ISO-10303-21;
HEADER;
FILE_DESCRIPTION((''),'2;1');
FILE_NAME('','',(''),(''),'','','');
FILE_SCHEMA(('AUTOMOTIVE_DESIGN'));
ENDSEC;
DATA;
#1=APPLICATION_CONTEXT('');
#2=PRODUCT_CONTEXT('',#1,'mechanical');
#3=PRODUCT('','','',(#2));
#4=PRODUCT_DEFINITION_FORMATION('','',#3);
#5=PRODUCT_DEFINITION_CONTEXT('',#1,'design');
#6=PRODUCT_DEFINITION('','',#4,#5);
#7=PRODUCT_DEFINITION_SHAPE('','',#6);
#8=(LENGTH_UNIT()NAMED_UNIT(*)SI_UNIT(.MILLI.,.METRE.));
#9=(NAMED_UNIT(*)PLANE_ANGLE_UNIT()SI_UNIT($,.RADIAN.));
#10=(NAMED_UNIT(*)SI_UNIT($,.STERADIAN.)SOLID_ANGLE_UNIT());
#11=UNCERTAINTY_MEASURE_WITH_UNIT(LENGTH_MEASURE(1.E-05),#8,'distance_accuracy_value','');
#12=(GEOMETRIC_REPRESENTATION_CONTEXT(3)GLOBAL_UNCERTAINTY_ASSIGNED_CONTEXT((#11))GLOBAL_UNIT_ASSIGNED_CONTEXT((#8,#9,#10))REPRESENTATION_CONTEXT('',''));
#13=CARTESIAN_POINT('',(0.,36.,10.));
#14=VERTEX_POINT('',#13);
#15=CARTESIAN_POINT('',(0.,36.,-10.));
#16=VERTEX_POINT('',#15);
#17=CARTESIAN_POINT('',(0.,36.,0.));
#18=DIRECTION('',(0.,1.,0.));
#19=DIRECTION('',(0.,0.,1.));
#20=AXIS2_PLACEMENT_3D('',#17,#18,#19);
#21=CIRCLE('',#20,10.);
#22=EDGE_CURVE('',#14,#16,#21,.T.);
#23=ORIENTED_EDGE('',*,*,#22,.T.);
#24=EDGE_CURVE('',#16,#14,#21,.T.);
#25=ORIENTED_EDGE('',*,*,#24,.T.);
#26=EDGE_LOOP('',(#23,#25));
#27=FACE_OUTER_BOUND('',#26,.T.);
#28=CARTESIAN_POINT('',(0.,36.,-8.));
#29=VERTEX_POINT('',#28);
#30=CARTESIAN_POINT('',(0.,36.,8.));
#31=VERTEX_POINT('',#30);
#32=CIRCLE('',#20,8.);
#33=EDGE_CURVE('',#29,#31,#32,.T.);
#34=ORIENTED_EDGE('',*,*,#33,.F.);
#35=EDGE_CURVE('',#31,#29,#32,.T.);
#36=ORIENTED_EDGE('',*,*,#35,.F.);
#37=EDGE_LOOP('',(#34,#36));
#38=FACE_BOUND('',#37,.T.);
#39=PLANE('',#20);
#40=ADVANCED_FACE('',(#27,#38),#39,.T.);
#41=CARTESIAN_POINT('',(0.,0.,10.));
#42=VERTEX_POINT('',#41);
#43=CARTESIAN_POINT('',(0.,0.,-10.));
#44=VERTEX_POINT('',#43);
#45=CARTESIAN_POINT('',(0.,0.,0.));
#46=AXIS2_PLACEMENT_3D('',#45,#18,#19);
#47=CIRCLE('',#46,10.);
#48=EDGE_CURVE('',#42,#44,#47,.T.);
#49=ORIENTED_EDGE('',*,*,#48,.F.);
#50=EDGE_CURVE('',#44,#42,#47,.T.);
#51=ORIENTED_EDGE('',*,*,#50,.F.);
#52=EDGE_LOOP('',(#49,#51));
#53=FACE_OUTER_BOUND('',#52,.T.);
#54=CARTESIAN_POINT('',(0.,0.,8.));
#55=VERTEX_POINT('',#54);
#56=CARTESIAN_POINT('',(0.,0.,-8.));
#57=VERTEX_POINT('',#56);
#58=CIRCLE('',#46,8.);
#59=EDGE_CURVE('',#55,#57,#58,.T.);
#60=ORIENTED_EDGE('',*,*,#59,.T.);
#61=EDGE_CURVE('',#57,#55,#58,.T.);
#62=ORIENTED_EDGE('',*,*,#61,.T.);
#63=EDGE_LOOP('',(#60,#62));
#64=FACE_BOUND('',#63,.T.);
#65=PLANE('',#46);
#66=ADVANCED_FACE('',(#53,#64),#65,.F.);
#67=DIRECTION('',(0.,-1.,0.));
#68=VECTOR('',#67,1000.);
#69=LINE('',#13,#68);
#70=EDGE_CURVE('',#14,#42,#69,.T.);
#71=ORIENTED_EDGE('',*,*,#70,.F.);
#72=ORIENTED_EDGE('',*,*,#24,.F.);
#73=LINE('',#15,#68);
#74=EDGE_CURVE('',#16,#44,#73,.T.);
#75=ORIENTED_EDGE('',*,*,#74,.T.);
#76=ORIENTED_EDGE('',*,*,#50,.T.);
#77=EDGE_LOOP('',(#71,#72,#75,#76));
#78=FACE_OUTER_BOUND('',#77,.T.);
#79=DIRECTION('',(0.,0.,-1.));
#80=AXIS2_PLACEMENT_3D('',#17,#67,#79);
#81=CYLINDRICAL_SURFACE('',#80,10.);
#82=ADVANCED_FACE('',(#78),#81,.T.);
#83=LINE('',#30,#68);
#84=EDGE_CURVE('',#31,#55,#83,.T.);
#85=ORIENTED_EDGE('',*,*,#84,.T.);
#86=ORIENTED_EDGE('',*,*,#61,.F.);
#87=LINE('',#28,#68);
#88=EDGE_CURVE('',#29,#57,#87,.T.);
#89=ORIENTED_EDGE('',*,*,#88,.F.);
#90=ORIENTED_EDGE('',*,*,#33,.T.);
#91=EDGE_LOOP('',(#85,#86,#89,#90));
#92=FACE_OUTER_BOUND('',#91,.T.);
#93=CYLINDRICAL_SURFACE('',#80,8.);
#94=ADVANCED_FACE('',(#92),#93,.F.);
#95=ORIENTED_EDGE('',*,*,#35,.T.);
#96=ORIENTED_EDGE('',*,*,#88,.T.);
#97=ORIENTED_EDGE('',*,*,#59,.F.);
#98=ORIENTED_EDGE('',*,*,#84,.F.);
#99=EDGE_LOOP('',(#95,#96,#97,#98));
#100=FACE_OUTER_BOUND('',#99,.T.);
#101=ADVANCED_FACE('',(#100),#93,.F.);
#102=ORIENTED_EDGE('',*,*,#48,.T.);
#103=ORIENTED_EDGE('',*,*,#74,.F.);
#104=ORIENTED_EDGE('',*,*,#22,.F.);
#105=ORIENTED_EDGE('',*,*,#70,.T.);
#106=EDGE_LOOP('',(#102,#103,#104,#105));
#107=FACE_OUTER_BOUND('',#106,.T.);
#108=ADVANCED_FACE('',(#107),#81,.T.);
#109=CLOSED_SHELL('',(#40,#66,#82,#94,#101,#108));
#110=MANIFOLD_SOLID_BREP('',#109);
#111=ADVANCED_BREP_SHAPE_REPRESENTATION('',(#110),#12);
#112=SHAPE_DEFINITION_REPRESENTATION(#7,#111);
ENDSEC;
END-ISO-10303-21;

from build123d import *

# Parameters (mm, degrees)
SKETCH1_R           = 10
SKETCH1_R_2         = 8
BOSS_EXTRUDE1_DEPTH = 36


with BuildPart() as part:
    # Sketch1 → Boss-Extrude1 (new body)
    with BuildSketch(Plane(origin=(0, 0, 0), x_dir=(1, 0, 0), z_dir=(0, 1, 0))):
        with Locations(Location((0, 0, 0), (0, 0, 270))):
            Circle(SKETCH1_R)
        with Locations(Location((0, 0, 0), (0, 0, 270))):
            Circle(SKETCH1_R_2, mode=Mode.SUBTRACT)
    extrude(amount=BOSS_EXTRUDE1_DEPTH)


solid = part.part
